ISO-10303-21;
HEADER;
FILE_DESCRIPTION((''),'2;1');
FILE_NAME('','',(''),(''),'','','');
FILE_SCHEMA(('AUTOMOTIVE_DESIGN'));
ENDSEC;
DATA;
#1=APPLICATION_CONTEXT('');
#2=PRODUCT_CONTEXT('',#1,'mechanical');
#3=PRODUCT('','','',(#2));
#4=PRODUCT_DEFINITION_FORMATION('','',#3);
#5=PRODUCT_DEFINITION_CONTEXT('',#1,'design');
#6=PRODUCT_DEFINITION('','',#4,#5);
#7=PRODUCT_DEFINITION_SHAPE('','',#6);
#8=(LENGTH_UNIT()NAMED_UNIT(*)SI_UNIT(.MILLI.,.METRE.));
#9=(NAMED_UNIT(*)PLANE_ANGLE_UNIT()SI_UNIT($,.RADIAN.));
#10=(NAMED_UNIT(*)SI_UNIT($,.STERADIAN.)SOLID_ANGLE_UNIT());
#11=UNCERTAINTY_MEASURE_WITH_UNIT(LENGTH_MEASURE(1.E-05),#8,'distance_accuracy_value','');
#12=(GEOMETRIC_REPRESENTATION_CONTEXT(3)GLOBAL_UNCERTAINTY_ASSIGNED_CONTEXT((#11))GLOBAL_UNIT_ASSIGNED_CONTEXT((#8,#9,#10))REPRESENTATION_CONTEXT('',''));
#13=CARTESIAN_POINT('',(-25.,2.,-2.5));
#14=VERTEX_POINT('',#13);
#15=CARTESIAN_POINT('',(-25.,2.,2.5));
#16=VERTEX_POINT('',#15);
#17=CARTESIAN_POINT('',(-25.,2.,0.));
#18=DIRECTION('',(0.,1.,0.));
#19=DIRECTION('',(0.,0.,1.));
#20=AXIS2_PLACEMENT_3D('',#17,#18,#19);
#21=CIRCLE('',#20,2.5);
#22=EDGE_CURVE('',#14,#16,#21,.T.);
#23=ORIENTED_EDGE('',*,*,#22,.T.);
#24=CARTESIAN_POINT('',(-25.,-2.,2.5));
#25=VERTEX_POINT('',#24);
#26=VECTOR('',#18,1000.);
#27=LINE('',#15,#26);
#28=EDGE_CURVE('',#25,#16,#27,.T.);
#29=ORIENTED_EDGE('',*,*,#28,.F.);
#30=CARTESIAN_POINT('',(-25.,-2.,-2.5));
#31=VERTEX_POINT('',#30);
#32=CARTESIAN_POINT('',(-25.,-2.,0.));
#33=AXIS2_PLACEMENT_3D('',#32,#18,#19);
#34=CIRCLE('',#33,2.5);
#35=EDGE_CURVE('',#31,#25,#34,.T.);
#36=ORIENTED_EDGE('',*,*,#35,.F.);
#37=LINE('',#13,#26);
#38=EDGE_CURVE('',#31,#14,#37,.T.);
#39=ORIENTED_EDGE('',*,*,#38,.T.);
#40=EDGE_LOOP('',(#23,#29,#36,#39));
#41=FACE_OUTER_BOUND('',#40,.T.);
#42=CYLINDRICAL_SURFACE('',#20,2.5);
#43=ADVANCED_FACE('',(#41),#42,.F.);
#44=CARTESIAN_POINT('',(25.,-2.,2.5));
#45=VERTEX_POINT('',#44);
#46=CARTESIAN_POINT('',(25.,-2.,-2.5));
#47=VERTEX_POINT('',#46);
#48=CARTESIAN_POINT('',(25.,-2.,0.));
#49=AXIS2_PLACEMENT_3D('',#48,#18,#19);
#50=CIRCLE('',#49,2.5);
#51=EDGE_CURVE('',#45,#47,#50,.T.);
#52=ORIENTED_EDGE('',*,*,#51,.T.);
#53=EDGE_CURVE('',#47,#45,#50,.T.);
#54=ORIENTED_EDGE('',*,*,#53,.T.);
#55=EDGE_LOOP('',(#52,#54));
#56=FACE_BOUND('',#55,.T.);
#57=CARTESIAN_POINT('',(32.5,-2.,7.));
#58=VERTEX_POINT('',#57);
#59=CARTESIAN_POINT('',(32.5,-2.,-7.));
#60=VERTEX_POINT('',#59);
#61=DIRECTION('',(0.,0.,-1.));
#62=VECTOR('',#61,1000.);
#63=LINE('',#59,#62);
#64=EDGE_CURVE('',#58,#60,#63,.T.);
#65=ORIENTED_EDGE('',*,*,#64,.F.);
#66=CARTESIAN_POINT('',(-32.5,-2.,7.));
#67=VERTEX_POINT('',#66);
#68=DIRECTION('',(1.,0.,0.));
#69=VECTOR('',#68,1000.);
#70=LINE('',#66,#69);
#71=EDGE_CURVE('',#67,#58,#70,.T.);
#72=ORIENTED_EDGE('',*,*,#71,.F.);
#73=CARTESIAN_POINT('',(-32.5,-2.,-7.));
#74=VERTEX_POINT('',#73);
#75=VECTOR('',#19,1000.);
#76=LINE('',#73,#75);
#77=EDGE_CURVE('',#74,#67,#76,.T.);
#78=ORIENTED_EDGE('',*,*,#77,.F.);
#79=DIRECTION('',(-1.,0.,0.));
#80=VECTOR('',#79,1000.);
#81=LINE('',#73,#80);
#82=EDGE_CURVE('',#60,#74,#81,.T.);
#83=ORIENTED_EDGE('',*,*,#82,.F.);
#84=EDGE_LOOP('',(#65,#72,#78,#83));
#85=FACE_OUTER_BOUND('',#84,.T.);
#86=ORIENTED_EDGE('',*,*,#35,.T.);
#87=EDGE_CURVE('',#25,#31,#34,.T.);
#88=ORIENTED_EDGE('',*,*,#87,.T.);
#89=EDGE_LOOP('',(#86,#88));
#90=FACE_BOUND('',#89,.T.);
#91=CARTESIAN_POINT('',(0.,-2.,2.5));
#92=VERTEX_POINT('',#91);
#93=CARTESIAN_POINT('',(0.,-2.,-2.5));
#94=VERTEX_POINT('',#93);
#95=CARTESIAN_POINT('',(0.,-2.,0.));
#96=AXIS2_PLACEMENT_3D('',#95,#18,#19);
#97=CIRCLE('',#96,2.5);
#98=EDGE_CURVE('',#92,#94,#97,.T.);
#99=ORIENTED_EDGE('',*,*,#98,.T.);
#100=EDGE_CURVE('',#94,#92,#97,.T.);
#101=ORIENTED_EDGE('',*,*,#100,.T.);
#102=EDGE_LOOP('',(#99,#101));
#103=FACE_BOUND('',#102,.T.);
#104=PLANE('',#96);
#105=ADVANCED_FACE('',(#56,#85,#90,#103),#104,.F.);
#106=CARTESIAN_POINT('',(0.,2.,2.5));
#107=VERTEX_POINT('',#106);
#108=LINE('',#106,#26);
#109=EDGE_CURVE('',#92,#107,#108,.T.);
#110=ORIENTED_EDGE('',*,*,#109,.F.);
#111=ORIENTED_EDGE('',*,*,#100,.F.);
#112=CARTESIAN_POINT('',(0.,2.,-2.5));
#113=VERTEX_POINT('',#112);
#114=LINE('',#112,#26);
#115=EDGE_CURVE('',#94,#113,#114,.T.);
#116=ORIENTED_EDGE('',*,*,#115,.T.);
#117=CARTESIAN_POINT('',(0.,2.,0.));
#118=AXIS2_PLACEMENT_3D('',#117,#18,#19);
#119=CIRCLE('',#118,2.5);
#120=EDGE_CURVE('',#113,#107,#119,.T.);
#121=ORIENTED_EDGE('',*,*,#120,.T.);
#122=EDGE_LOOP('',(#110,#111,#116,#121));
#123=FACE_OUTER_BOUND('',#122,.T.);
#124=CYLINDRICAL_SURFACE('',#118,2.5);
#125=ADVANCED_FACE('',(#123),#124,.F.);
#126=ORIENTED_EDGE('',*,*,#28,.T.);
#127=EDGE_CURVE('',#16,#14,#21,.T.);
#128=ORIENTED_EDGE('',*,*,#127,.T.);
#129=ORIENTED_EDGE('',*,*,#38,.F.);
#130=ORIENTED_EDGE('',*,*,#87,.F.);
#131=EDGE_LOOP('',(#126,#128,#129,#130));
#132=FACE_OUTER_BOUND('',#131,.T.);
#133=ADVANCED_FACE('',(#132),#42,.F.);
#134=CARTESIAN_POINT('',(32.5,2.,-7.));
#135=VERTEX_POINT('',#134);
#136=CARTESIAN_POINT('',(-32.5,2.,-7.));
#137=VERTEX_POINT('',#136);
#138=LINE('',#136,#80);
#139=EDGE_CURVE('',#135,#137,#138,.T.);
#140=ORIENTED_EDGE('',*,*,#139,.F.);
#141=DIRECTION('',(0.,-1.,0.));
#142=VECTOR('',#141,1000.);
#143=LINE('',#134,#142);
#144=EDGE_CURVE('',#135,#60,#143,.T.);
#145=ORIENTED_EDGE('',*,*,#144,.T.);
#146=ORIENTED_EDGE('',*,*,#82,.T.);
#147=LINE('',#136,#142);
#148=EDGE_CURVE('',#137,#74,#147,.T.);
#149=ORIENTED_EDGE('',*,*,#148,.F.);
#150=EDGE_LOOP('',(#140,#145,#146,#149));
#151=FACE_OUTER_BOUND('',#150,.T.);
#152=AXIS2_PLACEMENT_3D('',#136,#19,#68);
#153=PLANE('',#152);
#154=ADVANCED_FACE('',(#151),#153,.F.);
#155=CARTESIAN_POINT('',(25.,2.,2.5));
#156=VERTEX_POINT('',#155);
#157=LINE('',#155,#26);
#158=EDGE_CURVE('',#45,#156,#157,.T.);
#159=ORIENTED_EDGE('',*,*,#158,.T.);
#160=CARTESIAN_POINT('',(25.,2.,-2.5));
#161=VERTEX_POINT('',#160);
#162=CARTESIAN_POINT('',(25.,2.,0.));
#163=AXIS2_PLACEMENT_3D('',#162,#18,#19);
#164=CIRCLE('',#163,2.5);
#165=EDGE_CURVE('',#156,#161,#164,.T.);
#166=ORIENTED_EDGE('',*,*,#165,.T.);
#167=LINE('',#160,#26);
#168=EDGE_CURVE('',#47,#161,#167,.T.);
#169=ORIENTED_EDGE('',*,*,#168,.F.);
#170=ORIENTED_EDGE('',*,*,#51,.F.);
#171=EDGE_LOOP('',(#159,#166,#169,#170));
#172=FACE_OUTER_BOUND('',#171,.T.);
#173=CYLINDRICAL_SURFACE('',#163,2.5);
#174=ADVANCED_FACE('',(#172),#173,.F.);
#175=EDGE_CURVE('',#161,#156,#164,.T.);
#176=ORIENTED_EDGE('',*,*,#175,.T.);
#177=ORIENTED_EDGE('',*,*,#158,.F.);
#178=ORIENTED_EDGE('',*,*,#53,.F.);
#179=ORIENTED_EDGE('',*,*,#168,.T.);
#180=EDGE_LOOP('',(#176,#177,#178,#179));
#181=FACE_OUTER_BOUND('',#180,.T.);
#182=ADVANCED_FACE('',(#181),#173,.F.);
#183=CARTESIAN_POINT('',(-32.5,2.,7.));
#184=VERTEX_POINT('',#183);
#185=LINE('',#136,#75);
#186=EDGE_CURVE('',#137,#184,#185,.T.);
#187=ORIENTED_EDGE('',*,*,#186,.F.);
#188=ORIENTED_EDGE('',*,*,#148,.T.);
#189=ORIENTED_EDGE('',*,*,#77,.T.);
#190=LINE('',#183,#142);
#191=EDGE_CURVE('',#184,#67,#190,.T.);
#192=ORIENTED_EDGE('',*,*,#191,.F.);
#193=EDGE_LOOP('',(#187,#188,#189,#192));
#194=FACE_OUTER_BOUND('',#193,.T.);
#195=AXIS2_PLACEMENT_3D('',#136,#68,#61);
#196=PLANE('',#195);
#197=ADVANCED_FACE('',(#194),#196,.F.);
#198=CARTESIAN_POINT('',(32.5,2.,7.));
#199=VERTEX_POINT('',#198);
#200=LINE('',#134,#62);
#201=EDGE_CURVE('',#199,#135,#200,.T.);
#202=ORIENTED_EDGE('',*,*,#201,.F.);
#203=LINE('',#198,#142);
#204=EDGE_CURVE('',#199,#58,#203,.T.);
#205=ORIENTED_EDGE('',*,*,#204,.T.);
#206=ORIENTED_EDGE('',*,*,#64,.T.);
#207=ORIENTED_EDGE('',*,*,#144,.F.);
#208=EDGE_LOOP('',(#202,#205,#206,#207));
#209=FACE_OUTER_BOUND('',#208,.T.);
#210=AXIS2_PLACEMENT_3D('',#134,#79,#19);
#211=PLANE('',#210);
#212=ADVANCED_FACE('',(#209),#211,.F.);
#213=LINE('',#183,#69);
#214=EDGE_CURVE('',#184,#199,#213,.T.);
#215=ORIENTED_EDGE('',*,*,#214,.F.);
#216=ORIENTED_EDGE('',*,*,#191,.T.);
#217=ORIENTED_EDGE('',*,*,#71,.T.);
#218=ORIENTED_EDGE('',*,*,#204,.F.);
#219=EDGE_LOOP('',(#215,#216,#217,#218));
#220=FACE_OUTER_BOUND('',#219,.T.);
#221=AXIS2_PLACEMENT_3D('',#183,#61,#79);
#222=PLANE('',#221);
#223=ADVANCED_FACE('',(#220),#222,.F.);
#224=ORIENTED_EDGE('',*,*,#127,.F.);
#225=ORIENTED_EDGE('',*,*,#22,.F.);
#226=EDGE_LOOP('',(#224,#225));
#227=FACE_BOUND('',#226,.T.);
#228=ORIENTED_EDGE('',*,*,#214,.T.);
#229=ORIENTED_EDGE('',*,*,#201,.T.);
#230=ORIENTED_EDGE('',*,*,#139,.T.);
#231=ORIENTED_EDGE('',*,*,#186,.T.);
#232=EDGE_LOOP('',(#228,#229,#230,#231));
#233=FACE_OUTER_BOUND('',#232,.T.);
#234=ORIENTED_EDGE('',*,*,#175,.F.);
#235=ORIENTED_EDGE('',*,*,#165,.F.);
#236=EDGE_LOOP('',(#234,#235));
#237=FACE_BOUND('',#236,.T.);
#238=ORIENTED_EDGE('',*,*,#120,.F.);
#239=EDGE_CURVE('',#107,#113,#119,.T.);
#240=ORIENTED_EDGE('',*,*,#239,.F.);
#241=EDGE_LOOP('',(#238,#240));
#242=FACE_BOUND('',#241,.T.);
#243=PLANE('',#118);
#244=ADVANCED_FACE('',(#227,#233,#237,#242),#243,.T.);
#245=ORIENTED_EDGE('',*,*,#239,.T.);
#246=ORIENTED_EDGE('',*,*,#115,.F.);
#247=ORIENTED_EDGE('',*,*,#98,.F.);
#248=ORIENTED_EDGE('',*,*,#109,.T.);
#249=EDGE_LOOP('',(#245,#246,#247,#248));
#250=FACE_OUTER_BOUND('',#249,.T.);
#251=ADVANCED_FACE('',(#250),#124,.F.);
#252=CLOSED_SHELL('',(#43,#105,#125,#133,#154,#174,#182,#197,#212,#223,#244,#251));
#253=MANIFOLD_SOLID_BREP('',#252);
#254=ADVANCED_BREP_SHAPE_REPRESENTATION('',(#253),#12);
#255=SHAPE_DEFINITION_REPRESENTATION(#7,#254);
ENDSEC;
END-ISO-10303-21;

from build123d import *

# Parameters (mm, degrees)
SKETCH_2_W         = 65
SKETCH_2_H         = 14
EXTRUDE_1_DEPTH    = 2
HOLE_WIZARD_M6_1_D = 5


with BuildPart() as part:
    # 草图2 → 凸台-拉伸1 (new, symmetric)
    with BuildSketch(Plane(origin=(0, 0, 0), x_dir=(1, 0, 0), z_dir=(0, 1, 0))):
        Rectangle(SKETCH_2_W, SKETCH_2_H)
    extrude(amount=EXTRUDE_1_DEPTH, both=True)

    # M6 螺纹孔1 (through all)
    with Locations(Plane(origin=(0, 2, 0), x_dir=(1, 0, 0), z_dir=(0, 1, 0))):
        with Locations((-25, 0), (0, 0), (25, 0)):
            Hole(HOLE_WIZARD_M6_1_D / 2)


solid = part.part
